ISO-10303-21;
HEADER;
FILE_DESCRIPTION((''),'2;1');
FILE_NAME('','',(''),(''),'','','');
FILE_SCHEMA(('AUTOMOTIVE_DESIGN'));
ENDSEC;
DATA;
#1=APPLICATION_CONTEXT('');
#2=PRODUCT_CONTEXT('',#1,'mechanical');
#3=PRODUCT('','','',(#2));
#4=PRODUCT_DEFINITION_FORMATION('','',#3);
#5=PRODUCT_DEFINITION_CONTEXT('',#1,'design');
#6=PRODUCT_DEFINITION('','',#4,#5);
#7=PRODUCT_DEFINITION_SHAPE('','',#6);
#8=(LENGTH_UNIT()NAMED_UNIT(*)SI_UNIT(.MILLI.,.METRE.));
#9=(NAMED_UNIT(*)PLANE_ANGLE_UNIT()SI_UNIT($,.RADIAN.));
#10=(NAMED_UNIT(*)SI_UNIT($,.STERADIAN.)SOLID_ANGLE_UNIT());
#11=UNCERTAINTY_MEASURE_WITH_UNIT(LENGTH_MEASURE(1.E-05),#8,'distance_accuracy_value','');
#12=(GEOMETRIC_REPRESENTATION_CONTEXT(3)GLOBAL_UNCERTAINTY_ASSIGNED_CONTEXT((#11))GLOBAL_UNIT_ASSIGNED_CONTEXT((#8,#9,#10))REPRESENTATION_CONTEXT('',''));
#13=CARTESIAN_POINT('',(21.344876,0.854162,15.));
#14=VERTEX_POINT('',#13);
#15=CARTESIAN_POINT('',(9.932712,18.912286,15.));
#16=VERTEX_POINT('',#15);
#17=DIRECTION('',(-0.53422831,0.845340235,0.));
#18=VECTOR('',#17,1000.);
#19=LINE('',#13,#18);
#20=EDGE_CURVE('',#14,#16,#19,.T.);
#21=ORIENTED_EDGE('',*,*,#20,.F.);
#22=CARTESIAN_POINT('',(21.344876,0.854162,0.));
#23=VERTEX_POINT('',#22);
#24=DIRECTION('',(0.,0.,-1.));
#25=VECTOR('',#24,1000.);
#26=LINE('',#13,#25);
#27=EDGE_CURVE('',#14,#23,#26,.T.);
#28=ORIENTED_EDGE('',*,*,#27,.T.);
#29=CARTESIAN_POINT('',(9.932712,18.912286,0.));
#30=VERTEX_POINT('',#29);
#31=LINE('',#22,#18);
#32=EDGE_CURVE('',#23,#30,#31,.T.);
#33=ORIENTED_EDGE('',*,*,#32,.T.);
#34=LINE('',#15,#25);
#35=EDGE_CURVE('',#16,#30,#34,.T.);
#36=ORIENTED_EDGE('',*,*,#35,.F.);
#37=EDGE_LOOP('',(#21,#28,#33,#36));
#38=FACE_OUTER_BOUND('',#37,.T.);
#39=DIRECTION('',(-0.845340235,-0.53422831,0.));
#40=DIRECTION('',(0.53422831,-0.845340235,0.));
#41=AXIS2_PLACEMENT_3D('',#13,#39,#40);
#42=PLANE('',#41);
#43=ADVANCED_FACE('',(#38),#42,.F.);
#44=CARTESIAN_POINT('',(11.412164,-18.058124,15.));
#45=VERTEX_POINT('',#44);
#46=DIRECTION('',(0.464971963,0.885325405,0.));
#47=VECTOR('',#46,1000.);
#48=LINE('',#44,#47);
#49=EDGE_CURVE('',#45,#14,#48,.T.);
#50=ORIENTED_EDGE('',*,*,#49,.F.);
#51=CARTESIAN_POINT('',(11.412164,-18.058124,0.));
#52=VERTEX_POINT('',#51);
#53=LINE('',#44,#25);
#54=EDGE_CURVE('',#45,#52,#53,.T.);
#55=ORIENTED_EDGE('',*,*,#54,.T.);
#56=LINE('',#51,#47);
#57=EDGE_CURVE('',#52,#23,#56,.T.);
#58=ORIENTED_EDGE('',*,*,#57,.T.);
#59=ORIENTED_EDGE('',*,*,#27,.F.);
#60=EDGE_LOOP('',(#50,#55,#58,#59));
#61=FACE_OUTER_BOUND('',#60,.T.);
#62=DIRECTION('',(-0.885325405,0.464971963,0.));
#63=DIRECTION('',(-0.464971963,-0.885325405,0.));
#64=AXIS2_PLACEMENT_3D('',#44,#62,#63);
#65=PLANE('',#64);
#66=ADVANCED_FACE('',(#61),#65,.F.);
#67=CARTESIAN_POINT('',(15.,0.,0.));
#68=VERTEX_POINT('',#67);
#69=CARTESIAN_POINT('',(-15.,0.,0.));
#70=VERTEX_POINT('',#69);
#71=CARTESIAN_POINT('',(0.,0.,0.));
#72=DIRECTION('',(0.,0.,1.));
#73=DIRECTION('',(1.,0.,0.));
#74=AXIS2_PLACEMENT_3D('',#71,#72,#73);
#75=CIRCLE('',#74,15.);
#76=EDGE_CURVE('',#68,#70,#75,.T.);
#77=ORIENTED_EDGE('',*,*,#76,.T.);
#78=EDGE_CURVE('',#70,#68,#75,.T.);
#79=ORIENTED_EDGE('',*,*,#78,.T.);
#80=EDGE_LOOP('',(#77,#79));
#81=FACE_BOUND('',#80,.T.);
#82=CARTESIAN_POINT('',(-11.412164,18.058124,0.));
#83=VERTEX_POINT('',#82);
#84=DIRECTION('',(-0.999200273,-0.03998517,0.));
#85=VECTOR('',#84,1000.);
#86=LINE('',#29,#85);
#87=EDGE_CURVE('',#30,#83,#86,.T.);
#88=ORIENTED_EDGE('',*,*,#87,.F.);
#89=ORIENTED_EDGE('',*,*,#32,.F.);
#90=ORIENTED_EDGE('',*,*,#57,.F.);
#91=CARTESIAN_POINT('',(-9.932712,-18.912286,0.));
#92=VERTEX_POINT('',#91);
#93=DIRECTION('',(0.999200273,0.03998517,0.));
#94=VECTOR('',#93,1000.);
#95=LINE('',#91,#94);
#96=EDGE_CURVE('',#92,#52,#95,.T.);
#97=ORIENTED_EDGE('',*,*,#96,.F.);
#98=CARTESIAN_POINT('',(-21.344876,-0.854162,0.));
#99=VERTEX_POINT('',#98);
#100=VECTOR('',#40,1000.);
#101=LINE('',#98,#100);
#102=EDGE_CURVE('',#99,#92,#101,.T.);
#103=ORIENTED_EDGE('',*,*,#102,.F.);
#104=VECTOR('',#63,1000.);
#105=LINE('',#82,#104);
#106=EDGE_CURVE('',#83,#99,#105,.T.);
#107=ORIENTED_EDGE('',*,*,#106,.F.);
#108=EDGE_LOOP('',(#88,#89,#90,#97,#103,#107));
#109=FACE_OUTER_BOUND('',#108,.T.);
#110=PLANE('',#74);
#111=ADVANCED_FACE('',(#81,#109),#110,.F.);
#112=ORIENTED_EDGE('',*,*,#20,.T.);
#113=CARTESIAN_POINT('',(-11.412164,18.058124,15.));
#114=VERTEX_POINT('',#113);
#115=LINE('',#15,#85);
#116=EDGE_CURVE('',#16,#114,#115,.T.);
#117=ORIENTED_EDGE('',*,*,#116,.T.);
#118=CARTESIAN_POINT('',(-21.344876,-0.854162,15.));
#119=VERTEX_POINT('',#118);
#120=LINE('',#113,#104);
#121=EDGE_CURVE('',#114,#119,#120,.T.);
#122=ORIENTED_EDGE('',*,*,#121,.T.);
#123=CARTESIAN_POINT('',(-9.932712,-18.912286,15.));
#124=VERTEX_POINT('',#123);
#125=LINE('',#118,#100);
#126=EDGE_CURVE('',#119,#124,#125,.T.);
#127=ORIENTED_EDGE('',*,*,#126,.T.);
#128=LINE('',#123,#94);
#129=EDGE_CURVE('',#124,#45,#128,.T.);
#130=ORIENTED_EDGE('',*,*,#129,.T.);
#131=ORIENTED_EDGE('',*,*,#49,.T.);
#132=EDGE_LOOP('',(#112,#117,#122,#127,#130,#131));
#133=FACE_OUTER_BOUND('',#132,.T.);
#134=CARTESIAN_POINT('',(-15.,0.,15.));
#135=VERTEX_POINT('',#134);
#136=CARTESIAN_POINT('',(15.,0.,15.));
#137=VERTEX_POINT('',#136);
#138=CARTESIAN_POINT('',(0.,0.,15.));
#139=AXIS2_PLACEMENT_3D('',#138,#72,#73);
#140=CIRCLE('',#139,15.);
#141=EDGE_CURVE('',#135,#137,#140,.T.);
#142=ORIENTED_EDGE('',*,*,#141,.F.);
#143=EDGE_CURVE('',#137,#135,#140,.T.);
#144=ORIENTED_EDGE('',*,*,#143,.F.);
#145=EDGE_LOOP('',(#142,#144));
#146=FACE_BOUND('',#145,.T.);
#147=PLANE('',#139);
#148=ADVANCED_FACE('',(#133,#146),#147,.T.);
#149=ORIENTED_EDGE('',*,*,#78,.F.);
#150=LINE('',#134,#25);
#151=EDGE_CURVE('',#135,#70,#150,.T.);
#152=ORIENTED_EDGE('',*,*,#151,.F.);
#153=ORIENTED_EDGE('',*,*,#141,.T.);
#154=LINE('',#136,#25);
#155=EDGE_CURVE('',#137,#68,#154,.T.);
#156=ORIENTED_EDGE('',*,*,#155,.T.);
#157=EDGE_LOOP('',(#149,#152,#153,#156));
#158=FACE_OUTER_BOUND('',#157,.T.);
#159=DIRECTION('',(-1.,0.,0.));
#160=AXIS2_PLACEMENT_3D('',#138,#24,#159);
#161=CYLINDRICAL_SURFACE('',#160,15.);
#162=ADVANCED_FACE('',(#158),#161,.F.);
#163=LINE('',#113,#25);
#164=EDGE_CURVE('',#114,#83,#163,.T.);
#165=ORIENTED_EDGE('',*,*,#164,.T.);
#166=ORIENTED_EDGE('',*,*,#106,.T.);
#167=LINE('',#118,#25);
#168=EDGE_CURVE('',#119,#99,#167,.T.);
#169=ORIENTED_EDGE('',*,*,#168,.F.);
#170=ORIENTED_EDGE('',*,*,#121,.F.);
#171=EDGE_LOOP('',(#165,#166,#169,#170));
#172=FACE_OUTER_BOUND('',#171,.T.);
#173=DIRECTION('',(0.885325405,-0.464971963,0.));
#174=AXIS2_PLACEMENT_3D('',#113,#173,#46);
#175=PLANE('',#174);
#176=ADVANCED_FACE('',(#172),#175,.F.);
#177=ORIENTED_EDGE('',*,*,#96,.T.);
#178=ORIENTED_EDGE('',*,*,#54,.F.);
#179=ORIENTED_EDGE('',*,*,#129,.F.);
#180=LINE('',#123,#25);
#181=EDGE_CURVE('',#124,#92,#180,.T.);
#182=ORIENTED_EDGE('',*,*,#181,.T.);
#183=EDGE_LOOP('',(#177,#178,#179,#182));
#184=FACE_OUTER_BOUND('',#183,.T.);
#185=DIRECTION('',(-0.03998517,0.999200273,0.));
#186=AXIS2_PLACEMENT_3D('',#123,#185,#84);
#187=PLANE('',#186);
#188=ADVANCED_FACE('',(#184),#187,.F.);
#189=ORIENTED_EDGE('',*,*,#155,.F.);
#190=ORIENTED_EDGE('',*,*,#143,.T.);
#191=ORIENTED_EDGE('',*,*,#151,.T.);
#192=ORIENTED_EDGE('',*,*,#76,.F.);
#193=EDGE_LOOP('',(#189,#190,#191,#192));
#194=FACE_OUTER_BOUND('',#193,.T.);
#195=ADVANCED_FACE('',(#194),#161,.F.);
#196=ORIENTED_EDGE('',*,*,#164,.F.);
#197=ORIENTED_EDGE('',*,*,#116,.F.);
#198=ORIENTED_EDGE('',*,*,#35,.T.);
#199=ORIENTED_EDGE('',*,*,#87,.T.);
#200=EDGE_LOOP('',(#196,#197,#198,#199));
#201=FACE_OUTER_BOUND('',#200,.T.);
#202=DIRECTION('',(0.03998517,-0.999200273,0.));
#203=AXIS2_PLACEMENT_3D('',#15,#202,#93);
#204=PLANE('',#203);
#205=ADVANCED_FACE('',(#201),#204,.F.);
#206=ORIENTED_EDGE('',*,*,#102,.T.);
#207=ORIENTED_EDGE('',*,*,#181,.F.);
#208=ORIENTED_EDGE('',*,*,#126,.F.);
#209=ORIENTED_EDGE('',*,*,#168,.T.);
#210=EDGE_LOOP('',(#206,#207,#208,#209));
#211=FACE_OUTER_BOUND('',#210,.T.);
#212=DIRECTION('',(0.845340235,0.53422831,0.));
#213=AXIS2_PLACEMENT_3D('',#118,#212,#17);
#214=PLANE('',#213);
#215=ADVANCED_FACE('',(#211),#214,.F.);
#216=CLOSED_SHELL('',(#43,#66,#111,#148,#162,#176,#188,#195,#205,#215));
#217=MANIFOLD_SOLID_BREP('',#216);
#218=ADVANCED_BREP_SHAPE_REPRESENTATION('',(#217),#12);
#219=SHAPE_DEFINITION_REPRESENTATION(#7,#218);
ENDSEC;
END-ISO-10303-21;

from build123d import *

# Parameters (mm, degrees)
SKETCH1_R           = 15
BOSS_EXTRUDE1_DEPTH = 15


with BuildPart() as part:
    # Sketch1 → Boss-Extrude1 (new body)
    with BuildSketch(Plane.XY):
        Polygon((9.932712467, 18.912285858), (-11.412163764, 18.058124254), (-21.34487623, -0.854161605), (-9.932712467, -18.912285858), (11.412163764, -18.058124254), (21.34487623, 0.854161605), align=None)
        Circle(SKETCH1_R, mode=Mode.SUBTRACT)
    extrude(amount=BOSS_EXTRUDE1_DEPTH)


solid = part.part
